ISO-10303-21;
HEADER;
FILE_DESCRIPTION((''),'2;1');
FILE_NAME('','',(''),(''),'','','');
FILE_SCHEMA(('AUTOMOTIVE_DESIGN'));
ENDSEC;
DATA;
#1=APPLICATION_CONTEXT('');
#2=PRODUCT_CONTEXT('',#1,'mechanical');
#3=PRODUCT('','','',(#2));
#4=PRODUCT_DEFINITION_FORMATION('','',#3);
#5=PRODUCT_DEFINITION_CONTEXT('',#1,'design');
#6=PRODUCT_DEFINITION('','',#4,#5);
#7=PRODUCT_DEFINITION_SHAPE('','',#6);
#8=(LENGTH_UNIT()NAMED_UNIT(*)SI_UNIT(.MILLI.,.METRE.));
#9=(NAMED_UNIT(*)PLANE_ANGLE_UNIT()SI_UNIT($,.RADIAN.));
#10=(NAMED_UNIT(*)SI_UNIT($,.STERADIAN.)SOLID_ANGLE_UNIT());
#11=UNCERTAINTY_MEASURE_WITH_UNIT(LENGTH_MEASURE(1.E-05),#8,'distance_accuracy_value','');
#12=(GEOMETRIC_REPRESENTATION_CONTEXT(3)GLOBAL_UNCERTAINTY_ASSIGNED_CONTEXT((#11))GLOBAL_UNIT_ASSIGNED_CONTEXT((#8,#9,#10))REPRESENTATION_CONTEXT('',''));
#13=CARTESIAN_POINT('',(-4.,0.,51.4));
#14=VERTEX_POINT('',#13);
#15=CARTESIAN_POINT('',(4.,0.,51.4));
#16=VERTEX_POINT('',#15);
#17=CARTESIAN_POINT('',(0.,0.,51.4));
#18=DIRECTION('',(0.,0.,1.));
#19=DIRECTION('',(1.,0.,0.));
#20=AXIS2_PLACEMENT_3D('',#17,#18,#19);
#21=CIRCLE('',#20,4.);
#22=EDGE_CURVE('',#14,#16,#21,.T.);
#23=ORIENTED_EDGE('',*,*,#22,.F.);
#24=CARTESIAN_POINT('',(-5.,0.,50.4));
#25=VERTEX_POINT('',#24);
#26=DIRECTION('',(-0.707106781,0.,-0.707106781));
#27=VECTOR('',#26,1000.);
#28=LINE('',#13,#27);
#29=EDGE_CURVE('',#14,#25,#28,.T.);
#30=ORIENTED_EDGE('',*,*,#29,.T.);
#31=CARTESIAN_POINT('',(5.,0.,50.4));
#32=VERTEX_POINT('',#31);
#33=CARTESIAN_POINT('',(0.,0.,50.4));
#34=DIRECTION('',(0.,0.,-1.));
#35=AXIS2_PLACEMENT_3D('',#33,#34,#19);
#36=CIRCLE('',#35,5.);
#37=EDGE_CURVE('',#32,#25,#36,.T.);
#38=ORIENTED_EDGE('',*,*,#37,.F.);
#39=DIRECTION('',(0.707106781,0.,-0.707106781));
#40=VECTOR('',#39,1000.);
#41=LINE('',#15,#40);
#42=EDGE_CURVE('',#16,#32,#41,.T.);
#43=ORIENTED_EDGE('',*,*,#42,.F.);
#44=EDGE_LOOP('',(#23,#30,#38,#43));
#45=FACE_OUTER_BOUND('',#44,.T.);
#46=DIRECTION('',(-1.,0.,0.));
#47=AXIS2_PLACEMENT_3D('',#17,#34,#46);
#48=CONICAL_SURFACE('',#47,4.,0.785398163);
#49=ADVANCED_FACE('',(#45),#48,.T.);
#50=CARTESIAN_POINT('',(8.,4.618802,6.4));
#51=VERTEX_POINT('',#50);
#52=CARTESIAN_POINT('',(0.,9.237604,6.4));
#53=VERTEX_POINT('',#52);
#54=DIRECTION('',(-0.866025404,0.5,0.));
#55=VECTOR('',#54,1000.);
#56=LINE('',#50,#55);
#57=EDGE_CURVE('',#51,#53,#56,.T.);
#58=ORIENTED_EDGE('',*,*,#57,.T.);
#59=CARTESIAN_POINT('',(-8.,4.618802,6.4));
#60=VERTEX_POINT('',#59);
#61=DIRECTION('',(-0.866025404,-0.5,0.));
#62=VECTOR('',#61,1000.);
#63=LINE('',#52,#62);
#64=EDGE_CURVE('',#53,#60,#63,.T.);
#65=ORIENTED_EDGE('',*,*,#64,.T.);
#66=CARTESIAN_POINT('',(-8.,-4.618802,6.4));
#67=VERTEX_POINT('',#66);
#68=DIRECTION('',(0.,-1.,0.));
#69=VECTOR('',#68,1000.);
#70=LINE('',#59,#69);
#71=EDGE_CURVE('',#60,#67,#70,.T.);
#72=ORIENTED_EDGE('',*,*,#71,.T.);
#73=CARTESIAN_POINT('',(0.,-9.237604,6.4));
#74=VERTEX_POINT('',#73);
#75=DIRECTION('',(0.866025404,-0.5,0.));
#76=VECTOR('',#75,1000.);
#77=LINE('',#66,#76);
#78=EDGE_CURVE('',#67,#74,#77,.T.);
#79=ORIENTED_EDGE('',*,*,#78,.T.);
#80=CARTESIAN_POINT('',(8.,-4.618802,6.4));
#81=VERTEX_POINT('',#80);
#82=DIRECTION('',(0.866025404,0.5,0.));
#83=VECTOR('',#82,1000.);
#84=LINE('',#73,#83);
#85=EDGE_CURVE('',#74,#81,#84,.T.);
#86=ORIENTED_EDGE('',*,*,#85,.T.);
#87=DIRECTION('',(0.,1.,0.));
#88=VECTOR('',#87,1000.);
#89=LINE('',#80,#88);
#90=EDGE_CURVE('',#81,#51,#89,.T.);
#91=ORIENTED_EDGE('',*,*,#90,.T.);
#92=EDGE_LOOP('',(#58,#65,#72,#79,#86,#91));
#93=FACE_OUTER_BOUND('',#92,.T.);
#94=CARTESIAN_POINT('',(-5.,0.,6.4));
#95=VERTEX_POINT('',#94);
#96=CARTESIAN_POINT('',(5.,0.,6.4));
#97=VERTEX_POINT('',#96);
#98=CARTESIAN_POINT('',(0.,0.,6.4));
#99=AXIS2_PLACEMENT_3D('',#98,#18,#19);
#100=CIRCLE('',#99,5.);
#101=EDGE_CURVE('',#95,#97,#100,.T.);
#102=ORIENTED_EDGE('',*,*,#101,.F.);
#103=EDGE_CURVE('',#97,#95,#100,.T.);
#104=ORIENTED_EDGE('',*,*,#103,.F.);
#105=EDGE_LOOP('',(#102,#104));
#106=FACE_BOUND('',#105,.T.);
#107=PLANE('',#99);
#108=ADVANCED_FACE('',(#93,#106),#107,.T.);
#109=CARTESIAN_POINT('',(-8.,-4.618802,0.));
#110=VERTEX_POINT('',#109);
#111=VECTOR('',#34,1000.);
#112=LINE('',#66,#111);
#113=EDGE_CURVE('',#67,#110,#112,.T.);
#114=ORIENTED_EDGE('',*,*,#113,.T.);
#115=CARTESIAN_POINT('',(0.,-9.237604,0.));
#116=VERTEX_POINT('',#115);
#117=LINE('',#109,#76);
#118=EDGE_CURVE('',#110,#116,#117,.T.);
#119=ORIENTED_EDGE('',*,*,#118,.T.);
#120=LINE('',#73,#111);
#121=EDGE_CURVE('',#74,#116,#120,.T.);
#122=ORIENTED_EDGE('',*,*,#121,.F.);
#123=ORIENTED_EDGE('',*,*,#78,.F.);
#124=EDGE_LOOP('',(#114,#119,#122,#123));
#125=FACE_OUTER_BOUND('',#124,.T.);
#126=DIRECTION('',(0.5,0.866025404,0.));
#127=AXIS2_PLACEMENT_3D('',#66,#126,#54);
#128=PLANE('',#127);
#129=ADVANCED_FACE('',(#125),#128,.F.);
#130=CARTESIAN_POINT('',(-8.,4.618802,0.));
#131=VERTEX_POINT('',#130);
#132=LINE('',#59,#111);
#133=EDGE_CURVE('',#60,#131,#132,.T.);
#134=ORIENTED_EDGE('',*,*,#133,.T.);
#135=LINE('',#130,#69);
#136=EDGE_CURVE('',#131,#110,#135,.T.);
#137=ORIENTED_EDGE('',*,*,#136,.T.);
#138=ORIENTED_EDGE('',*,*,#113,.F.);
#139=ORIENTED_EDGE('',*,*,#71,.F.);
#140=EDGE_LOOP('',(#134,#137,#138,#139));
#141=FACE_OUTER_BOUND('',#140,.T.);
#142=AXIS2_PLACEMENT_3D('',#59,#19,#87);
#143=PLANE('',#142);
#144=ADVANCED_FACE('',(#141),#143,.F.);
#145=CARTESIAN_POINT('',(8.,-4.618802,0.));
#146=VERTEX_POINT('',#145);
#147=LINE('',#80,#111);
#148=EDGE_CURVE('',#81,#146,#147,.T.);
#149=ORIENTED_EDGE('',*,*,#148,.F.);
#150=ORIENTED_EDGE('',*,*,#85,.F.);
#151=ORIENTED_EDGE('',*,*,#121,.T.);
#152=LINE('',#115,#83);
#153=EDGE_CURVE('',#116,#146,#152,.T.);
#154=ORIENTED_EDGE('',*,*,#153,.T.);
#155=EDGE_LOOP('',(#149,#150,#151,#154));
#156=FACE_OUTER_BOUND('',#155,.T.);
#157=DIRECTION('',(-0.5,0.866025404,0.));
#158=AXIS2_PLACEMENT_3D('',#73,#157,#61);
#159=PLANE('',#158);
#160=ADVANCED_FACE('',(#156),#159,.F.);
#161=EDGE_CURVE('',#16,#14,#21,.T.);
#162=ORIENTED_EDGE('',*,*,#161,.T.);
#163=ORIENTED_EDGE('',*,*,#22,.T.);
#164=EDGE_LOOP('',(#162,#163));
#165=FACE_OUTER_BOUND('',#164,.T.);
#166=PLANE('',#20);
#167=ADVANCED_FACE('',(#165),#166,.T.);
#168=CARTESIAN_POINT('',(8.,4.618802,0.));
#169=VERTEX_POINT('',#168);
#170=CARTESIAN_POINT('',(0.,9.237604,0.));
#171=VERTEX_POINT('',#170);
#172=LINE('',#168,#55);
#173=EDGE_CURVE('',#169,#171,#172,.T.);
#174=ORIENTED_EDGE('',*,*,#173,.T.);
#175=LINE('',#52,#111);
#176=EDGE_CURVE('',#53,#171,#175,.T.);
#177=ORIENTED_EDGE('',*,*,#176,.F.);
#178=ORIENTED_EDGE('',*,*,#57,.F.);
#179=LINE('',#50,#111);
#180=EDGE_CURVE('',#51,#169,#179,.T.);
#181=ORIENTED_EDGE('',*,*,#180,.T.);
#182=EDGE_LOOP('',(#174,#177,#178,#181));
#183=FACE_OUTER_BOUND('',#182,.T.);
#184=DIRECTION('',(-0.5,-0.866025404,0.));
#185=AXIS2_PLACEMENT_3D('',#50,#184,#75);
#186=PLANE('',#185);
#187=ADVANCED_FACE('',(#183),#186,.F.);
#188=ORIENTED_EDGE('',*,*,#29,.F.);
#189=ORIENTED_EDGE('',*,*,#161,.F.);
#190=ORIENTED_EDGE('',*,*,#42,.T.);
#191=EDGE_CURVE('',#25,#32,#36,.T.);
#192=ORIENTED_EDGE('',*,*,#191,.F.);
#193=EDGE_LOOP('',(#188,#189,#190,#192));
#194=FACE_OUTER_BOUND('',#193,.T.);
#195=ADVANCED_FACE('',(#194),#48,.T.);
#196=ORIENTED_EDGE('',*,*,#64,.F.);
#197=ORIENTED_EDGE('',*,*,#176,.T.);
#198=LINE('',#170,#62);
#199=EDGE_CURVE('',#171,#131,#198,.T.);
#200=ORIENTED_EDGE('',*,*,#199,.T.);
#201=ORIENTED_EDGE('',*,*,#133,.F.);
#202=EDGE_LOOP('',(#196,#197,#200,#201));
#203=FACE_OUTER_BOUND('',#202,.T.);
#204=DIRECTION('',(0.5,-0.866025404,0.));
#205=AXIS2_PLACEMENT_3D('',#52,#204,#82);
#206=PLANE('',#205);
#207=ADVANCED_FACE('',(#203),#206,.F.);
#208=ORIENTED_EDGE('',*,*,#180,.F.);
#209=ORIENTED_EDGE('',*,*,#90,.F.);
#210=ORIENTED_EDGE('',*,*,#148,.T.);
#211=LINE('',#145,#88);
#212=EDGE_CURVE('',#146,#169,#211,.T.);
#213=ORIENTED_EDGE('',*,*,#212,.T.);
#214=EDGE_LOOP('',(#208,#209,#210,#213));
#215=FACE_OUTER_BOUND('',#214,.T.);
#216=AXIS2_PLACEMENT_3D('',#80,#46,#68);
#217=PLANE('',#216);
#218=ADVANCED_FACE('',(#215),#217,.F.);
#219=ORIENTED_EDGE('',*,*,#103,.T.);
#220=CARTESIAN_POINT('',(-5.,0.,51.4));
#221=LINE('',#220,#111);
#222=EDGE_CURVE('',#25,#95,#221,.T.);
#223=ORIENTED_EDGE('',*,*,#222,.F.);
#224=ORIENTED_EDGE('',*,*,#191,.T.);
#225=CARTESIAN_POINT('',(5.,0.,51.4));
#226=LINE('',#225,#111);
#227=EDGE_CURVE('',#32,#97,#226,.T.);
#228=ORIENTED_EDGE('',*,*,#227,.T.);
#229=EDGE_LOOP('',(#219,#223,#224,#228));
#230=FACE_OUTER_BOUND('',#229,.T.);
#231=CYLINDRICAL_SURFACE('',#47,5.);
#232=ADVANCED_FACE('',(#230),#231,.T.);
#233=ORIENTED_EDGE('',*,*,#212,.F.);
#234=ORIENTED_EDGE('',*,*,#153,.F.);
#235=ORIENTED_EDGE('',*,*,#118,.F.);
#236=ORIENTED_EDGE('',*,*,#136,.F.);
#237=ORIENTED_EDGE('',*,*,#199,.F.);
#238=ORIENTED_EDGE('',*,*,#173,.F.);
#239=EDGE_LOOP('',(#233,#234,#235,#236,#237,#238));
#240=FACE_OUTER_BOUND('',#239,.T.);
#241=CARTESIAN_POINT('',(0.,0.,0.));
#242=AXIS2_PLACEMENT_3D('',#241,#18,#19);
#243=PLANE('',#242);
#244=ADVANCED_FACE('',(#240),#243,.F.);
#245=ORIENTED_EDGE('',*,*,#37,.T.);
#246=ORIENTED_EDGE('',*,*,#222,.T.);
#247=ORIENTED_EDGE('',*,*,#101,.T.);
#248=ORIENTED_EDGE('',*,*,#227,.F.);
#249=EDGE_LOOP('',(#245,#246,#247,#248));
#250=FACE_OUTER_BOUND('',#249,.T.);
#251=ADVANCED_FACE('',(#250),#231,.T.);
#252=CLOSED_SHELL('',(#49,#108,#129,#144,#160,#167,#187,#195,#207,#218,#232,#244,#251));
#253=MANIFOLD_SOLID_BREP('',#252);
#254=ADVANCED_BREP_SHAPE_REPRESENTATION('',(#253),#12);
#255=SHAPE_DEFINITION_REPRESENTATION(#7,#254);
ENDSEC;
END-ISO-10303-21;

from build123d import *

# Parameters (mm, degrees)
BOSS_EXTRUDE1_DEPTH = 6.4
SKETCH3_R           = 5
BOSS_EXTRUDE2_DEPTH = 45
CHAMFER1_SIZE       = 1


with BuildPart() as part:
    # Sketch1 → Boss-Extrude1 (new body)
    with BuildSketch(Plane.XY):
        Polygon((8, 4.618802154), (0, 9.237604307), (-8, 4.618802154), (-8, -4.618802154), (0, -9.237604307), (8, -4.618802154), align=None)
    extrude(amount=BOSS_EXTRUDE1_DEPTH)

    # Sketch3 → Boss-Extrude2 (add)
    with BuildSketch(Plane.XY.offset(6.4)):
        with Locations(Location((0, 0, 0), (0, 0, 180))):
            Circle(SKETCH3_R)
    extrude(amount=BOSS_EXTRUDE2_DEPTH)

    # Chamfer1
    chamfer1_edges = [part.edges().sort_by_distance(p)[0] for p in [
        (5, 0, 51.4),
    ]]
    chamfer(chamfer1_edges, length=CHAMFER1_SIZE)


solid = part.part
